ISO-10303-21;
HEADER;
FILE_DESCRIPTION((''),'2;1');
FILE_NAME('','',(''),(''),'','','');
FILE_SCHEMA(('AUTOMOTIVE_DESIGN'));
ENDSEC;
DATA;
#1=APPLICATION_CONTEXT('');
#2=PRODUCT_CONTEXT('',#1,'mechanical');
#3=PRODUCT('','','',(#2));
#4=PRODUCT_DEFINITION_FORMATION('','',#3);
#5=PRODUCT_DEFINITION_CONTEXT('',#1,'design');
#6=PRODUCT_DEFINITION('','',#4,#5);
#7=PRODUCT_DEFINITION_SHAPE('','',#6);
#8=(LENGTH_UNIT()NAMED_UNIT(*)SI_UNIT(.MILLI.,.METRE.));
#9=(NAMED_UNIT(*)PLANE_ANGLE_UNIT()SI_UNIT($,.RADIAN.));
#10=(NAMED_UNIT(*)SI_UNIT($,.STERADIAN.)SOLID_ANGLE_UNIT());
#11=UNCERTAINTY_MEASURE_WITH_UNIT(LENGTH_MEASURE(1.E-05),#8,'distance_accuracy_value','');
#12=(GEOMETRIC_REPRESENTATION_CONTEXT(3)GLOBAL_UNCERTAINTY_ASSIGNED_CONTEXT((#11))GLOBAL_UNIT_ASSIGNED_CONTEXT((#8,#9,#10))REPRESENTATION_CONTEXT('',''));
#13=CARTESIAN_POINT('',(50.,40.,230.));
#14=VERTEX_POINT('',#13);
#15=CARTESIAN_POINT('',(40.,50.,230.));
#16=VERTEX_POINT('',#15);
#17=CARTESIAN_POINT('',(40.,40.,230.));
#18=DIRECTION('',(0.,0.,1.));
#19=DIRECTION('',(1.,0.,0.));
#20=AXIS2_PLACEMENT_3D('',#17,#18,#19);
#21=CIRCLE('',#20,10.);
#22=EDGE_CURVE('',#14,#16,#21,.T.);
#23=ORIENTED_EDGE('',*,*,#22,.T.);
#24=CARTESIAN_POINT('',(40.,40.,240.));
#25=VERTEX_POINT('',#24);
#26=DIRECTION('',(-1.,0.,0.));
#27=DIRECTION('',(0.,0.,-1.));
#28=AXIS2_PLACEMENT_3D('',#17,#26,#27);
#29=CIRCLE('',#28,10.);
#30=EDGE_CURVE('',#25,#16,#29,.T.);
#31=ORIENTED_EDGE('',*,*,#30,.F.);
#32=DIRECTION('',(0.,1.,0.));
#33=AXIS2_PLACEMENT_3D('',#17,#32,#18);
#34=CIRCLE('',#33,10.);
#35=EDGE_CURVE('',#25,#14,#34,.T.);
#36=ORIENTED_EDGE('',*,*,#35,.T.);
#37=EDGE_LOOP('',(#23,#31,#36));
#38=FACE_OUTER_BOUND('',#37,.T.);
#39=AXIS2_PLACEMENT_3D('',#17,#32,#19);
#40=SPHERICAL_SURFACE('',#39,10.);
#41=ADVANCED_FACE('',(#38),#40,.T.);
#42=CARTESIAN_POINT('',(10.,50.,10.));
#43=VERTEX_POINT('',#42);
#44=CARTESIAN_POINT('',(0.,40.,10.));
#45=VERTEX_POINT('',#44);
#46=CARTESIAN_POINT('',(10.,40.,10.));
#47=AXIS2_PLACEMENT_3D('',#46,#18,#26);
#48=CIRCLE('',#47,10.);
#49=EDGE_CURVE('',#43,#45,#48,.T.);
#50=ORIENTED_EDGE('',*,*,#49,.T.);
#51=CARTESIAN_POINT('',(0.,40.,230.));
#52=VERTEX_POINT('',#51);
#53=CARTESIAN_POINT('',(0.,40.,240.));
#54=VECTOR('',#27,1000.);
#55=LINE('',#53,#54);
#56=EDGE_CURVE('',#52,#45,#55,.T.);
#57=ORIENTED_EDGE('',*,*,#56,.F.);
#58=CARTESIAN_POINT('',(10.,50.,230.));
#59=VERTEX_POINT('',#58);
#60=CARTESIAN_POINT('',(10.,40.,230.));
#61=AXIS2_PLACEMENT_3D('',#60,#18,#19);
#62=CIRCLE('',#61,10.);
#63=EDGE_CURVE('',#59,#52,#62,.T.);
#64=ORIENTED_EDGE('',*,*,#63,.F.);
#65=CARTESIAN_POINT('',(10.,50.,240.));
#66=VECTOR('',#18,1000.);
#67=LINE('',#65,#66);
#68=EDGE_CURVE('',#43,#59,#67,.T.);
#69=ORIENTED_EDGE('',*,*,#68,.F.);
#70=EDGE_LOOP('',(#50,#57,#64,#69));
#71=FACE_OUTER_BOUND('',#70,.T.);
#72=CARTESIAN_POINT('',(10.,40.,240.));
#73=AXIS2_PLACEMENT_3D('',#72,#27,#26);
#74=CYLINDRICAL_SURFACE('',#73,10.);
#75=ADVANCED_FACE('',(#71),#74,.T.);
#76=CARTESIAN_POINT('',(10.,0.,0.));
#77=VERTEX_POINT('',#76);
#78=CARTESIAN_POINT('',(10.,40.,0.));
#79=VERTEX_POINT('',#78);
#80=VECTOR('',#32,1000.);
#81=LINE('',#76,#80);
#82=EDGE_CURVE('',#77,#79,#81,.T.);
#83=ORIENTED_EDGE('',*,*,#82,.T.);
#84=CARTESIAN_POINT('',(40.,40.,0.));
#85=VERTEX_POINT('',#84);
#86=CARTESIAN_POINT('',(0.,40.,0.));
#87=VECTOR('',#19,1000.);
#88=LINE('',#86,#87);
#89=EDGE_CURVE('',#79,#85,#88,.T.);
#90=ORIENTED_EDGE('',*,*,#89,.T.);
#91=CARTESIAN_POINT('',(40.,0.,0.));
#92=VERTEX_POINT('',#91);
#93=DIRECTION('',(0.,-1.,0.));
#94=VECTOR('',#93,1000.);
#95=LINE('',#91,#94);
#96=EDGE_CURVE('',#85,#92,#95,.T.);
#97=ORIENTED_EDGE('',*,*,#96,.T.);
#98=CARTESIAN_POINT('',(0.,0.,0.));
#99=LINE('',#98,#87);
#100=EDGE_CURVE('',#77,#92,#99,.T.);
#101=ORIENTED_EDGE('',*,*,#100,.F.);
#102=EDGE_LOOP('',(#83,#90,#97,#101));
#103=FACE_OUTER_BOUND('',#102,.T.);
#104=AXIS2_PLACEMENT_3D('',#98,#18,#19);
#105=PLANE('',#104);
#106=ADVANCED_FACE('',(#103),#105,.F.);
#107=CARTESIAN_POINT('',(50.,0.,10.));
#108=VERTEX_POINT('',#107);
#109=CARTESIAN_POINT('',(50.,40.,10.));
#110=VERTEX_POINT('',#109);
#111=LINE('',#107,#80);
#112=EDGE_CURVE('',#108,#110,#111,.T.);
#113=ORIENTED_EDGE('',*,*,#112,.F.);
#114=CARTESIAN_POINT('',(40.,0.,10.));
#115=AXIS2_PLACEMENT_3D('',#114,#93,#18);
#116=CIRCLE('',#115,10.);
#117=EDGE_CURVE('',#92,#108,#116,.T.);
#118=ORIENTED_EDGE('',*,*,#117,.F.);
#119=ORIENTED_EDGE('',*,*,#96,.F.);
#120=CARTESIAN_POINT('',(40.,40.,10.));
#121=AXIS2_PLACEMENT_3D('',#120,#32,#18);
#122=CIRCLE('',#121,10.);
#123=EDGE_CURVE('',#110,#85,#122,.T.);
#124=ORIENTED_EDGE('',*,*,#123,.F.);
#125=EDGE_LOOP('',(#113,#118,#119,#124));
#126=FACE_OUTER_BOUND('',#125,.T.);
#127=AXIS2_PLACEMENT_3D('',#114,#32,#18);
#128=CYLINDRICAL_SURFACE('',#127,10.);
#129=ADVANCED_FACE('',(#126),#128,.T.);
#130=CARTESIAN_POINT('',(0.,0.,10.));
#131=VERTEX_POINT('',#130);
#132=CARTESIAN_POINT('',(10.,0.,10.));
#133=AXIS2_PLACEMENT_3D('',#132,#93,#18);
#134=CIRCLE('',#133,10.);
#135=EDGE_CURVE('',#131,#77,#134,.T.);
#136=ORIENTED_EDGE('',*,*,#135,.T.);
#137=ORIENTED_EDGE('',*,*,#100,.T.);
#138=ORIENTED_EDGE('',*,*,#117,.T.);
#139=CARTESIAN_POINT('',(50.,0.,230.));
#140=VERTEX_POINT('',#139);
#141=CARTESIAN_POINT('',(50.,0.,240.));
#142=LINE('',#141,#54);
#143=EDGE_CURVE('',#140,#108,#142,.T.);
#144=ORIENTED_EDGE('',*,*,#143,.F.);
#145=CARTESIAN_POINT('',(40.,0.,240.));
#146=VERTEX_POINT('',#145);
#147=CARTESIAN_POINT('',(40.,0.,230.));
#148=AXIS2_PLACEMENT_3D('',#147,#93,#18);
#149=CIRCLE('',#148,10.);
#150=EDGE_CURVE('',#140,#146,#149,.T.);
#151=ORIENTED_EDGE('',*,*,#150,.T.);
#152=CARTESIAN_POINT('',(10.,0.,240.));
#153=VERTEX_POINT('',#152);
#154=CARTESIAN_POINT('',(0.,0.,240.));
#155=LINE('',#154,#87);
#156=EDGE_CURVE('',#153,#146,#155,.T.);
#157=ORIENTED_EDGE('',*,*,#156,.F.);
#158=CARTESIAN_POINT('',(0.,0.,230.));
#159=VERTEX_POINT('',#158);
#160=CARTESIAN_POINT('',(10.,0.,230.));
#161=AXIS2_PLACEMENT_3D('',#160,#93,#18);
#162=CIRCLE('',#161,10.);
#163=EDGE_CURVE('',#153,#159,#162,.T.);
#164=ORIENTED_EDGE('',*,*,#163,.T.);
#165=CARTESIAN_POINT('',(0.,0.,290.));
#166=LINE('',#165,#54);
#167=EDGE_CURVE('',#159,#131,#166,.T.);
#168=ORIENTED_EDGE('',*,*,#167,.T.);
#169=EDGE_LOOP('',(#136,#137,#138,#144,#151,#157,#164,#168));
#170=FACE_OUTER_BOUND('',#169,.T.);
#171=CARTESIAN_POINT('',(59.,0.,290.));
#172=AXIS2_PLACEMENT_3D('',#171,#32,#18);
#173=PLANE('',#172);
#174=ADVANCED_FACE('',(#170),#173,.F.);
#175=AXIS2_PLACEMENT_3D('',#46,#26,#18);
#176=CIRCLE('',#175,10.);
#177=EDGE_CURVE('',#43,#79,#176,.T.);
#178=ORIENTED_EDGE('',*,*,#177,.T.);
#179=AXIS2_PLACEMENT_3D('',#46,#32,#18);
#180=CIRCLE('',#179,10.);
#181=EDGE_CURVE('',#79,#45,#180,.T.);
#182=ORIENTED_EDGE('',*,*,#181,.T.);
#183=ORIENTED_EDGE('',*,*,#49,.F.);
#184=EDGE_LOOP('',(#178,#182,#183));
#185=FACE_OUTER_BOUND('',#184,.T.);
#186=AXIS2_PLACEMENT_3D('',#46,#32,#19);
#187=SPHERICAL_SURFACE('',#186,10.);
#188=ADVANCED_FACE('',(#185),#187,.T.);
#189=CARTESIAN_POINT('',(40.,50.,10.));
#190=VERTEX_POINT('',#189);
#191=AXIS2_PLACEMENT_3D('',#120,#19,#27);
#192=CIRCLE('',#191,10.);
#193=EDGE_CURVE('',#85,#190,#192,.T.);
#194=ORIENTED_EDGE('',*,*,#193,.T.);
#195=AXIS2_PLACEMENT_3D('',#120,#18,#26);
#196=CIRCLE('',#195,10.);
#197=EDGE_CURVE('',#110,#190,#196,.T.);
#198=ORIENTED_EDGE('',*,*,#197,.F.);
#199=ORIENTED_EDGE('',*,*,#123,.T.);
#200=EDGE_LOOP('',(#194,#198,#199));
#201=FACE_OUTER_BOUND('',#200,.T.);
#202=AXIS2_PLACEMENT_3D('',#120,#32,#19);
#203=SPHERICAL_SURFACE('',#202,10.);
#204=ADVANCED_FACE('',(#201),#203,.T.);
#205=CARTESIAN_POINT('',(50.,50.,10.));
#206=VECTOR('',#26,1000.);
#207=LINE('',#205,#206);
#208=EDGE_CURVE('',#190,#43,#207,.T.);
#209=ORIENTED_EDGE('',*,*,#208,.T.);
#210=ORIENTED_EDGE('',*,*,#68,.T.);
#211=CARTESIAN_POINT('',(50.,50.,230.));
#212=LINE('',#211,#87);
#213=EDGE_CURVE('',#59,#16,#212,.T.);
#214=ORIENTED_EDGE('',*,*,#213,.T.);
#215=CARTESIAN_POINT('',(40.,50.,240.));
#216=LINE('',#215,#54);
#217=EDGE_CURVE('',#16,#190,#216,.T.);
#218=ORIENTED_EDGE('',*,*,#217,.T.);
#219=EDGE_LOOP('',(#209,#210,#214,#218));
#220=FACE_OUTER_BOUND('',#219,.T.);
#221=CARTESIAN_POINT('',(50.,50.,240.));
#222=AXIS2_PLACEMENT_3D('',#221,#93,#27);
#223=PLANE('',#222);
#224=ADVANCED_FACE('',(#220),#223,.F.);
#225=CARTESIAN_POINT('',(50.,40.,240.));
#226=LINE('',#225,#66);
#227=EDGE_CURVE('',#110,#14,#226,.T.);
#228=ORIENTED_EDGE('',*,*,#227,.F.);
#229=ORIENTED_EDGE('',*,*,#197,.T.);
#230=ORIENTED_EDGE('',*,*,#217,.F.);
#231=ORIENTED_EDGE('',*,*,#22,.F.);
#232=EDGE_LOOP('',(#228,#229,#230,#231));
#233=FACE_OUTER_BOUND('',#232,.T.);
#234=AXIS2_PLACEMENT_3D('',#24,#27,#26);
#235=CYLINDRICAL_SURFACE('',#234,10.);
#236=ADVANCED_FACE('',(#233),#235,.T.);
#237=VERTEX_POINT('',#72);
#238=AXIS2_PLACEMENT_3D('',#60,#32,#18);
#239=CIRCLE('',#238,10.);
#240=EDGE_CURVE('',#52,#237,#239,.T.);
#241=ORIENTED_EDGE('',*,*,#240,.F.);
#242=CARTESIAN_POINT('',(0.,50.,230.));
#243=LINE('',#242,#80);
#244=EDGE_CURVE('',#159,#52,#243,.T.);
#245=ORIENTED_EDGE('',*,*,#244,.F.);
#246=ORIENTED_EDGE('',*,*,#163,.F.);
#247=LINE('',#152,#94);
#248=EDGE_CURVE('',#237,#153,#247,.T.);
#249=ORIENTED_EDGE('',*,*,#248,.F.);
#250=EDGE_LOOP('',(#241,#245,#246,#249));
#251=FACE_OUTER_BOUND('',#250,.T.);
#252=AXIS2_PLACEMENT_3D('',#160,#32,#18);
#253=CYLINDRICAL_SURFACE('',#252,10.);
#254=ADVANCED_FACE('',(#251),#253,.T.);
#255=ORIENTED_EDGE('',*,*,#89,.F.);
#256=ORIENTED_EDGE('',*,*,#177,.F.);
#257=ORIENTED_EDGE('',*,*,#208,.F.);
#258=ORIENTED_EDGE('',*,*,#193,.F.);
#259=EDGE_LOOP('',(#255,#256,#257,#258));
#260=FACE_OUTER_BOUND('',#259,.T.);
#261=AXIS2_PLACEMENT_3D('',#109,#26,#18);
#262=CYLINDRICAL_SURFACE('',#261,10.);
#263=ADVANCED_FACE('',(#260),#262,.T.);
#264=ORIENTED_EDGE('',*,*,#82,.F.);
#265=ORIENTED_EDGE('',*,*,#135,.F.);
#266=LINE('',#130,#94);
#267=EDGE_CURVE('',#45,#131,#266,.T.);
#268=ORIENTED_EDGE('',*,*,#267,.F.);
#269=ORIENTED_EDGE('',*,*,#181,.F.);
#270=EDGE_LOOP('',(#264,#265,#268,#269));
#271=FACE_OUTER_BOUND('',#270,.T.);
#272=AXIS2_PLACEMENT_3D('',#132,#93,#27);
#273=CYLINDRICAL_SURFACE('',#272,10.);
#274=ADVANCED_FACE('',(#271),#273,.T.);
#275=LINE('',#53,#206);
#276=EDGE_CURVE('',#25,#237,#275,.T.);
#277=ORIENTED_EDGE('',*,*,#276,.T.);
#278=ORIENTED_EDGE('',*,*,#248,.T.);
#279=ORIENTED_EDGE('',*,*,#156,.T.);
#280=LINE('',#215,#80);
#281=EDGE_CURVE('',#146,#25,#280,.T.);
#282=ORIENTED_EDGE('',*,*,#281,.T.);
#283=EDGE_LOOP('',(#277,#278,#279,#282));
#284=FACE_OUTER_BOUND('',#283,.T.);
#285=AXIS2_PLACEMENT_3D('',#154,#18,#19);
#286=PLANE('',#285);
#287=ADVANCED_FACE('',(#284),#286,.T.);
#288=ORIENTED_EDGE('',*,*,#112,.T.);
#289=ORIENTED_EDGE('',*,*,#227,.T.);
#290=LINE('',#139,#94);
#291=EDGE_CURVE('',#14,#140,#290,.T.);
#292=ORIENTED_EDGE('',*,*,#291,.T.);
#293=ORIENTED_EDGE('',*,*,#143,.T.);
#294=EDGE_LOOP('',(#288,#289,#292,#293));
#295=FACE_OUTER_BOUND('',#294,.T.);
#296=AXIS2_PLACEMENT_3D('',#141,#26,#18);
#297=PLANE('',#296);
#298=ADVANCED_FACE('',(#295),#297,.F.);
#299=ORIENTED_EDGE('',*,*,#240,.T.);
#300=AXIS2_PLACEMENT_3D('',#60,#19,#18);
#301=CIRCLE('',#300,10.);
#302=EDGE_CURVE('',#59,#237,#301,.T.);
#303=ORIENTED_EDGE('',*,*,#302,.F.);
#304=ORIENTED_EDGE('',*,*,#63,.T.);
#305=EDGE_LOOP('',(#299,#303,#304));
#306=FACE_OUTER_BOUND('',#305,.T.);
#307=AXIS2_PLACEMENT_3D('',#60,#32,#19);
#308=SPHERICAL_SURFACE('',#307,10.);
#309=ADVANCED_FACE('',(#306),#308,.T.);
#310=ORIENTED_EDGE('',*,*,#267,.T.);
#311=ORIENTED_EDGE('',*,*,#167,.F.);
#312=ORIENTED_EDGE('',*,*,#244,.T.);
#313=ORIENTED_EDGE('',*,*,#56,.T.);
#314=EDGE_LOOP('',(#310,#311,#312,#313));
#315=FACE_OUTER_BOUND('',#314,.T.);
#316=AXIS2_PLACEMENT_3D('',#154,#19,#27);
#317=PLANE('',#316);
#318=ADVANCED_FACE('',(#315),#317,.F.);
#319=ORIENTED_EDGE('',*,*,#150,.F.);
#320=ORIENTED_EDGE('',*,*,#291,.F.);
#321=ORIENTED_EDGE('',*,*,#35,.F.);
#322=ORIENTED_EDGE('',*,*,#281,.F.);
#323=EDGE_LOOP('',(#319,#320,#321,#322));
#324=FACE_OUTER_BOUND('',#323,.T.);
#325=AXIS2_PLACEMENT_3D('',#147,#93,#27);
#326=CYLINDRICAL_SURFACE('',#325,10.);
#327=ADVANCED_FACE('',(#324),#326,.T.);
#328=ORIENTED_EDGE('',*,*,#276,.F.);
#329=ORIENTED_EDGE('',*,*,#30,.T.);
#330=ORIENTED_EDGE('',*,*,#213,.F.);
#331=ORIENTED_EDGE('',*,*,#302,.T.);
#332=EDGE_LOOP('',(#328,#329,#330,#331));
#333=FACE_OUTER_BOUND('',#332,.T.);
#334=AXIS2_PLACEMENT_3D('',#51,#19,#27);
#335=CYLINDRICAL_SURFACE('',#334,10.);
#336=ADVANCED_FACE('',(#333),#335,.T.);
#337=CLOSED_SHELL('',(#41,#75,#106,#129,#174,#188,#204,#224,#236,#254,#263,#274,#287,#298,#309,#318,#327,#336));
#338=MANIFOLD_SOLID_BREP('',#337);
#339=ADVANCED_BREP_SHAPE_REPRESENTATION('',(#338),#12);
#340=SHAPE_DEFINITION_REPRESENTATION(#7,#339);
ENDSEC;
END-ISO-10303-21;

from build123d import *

# Parameters (mm, degrees)
SKETCH_1_W          = 50
SKETCH_1_H          = 50
EXTRUDE_2_DEPTH     = 240
EXTRUDE_3_DEPTH     = 5
FILLET_1_R          = 10
SKETCH_3_W          = 340
SKETCH_3_H          = 5
CUT_EXTRUDE_1_DEPTH = 59


with BuildPart() as part:
    # 草图1 → 凸台-拉伸2 (new body)
    with BuildSketch(Plane.XY):
        with Locations((25, 25)):
            Rectangle(SKETCH_1_W, SKETCH_1_H)
    extrude(amount=EXTRUDE_2_DEPTH)

    # 草图2 → 凸台-拉伸3 (add)
    with BuildSketch(Plane.XZ):
        Polygon((0, 240), (0, 290), (50, 290), (50, 0), (50, -50), (0, -50), align=None)
    extrude(amount=EXTRUDE_3_DEPTH)

    # 圆角1
    fillet_1_edges = [part.edges().sort_by_distance(p)[0] for p in [
        (25, 50, 240),
        (0, 25, 240),
        (50, 25, 240),
        (50, 50, 120),
        (50, 25, 0),
        (0, 25, 0),
        (25, 50, 0),
        (0, 50, 120),
    ]]
    fillet(fillet_1_edges, radius=FILLET_1_R)

    # 草图3 → 切除-拉伸1 (cut)
    with BuildSketch(Plane.ZY):
        with Locations((120, -2.5)):
            Rectangle(SKETCH_3_W, SKETCH_3_H)
    extrude(amount=-CUT_EXTRUDE_1_DEPTH, mode=Mode.SUBTRACT)


solid = part.part
